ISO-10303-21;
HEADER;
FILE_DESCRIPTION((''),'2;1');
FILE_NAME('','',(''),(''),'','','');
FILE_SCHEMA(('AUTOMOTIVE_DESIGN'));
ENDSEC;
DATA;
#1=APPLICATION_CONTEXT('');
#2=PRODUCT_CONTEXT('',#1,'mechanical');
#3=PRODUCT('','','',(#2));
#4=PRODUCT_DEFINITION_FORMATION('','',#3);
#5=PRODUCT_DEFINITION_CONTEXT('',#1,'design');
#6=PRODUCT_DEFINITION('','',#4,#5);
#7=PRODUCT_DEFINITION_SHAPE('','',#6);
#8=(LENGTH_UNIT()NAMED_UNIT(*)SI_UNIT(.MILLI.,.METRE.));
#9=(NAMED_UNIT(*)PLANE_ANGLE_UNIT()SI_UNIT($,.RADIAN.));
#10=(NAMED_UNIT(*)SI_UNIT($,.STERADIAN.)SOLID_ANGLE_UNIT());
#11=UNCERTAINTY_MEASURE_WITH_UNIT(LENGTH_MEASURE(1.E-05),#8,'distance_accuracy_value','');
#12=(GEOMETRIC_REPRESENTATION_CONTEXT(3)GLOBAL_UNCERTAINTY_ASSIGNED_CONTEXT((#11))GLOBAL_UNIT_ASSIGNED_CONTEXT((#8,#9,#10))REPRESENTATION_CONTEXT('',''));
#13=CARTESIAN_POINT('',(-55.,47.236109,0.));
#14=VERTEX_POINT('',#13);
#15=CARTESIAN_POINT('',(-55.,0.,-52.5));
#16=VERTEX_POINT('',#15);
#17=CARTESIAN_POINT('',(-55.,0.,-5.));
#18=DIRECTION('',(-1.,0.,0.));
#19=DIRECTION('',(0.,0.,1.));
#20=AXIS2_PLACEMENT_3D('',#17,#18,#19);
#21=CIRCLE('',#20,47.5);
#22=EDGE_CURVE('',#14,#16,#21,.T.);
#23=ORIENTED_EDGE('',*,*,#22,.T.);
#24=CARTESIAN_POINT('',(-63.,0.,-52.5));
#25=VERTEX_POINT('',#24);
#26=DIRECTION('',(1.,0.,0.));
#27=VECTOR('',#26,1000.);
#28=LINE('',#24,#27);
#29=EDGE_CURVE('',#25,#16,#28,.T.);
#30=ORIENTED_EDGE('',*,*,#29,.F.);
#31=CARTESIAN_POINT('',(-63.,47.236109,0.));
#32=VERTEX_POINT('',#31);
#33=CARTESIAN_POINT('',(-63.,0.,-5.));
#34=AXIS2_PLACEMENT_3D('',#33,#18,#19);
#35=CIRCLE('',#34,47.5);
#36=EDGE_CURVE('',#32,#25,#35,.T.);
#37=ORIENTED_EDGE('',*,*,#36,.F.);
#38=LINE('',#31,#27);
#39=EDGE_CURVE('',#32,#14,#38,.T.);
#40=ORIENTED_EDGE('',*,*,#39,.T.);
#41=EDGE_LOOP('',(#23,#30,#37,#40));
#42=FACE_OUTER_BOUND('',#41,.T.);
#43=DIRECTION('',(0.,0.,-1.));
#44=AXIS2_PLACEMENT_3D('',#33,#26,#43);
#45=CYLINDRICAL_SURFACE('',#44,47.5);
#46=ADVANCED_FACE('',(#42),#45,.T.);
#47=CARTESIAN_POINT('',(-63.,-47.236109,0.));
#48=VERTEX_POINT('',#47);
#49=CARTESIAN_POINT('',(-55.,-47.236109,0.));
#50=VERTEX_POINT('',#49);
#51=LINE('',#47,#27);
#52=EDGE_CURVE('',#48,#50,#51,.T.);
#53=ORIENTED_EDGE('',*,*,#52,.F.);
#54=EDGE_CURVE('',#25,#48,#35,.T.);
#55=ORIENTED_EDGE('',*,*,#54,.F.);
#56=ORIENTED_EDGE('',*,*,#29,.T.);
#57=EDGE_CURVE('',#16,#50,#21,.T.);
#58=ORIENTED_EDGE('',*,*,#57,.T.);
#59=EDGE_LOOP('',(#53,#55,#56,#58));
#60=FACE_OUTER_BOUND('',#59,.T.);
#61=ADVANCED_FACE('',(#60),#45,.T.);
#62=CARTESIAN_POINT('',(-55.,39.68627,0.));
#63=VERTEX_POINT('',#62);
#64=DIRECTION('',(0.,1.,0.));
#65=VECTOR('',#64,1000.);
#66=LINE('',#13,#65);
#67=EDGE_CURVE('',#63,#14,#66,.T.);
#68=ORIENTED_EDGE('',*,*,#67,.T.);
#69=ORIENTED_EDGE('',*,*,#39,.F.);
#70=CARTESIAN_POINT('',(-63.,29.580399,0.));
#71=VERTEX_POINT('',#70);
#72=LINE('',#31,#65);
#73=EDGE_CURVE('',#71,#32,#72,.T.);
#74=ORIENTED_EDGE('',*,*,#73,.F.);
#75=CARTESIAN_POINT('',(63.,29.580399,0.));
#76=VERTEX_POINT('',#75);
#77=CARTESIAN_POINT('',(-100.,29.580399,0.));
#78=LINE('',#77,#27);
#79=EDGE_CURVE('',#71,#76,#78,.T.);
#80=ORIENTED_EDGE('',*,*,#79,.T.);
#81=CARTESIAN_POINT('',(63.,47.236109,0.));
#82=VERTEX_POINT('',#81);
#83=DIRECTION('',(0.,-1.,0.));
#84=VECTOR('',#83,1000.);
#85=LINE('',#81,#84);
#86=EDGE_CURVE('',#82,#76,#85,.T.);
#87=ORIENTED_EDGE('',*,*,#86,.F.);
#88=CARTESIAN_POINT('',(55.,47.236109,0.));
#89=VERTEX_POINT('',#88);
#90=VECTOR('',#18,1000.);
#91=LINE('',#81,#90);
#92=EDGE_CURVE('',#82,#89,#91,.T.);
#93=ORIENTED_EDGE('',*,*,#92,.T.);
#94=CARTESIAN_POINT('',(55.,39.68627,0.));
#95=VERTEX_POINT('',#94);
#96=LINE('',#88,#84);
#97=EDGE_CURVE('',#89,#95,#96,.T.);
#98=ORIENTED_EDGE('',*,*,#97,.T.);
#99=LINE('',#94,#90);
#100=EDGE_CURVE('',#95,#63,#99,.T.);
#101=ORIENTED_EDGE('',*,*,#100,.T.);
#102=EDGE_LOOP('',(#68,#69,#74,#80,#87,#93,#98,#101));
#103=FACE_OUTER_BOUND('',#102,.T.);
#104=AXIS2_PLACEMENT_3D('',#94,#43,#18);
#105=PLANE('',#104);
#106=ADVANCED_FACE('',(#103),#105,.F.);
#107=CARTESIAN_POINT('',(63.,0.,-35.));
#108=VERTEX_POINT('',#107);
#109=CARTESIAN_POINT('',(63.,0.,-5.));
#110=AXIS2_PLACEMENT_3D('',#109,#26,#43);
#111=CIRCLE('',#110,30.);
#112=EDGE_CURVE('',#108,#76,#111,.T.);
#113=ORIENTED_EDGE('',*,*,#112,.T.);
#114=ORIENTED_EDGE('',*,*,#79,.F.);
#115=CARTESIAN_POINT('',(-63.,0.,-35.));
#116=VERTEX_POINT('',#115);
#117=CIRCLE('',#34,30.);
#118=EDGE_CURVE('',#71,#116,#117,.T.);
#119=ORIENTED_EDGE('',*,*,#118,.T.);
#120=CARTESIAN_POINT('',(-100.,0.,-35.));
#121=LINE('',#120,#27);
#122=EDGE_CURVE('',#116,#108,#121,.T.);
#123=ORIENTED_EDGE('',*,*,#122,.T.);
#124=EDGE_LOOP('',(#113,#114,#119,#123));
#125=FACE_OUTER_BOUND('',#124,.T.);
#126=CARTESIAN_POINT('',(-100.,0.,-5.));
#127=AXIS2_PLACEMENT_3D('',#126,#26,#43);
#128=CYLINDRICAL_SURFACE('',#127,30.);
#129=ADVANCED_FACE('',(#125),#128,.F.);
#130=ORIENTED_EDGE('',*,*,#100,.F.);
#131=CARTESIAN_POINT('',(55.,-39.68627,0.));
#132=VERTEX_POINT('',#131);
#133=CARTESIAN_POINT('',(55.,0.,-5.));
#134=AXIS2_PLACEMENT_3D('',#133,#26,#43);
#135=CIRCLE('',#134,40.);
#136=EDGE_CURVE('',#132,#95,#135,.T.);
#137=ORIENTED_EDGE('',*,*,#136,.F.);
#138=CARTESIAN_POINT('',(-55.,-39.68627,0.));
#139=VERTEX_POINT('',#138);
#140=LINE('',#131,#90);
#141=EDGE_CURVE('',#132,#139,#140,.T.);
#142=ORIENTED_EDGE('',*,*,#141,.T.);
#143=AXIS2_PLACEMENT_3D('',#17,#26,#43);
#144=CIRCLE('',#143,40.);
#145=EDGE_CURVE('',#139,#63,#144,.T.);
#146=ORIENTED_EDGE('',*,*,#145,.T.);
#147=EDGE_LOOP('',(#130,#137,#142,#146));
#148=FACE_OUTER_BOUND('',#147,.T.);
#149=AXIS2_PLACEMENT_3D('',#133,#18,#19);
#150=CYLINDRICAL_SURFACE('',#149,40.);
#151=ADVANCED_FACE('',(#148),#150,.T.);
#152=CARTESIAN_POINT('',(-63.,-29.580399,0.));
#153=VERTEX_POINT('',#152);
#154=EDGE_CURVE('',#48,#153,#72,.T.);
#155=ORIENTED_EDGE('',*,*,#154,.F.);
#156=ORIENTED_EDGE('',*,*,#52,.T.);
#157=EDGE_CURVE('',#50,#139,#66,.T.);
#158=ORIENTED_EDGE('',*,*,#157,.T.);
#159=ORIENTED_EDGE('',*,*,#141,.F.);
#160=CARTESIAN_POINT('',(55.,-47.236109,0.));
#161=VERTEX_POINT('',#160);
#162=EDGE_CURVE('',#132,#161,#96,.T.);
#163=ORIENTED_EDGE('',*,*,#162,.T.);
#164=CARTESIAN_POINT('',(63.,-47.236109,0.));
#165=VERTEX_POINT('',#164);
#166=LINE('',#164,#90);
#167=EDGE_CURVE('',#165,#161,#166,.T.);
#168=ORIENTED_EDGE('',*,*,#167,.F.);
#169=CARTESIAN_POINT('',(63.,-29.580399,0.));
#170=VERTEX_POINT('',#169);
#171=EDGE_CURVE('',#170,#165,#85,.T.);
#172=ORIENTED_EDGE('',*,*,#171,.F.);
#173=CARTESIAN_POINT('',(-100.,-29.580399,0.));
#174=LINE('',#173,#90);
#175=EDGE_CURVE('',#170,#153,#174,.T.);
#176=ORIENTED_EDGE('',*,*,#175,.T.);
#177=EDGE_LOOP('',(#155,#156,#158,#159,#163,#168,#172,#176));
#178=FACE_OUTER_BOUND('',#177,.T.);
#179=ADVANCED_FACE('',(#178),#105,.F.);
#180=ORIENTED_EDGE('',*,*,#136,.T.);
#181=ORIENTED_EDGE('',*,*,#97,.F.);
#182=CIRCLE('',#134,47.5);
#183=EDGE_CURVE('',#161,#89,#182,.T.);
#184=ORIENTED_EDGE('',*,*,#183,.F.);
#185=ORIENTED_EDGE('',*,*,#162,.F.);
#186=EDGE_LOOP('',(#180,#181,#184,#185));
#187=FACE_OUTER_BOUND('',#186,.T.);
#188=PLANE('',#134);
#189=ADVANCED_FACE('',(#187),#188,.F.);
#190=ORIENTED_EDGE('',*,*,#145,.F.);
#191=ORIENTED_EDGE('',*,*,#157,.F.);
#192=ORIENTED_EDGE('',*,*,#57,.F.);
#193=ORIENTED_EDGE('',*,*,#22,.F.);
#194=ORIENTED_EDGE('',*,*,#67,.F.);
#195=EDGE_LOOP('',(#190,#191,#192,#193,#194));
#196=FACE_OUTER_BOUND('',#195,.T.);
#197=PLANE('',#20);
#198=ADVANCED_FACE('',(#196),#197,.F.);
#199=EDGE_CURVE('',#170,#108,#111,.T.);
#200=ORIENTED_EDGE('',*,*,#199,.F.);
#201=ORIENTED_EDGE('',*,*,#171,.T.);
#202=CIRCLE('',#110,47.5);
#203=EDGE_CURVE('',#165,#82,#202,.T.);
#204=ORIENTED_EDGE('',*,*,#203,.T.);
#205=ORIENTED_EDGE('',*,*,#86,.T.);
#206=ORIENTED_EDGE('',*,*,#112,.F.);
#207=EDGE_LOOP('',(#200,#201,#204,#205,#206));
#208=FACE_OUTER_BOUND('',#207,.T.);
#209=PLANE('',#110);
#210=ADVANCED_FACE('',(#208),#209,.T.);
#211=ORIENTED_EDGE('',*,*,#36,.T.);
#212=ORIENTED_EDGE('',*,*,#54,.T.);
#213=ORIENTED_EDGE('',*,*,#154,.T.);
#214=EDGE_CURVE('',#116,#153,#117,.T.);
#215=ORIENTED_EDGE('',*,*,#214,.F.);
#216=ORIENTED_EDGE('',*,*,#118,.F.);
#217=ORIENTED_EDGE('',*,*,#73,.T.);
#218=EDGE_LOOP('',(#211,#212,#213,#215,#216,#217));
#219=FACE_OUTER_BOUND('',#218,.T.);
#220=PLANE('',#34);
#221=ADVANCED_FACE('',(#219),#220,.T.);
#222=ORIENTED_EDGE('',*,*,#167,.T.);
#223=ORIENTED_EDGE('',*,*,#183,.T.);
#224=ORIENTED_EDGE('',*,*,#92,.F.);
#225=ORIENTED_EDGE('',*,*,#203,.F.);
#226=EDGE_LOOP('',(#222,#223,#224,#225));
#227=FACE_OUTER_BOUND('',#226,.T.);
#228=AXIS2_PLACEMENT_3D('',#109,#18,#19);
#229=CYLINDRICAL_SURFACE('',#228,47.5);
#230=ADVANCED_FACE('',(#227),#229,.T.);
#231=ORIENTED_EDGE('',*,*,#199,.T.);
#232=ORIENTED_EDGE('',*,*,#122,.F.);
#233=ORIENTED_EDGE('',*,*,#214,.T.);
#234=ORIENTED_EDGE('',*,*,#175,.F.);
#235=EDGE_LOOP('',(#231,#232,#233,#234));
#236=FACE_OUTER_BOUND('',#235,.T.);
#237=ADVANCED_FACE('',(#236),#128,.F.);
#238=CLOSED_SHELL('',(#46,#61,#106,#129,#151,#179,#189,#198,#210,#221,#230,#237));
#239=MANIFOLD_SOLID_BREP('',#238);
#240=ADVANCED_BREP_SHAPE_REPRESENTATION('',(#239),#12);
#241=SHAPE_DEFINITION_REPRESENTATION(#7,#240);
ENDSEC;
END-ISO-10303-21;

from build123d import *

# Parameters (mm, degrees)
HALF_SHELL_BODY_DEPTH   = 55
END_FLANGE_B_95X8_DEPTH = 8
END_START               = 8
END_FLANGE_A_95X8_DEPTH = 8
BORE_SKETCH_60_R        = 30
BORE_CUT_60_DEPTH       = 100


with BuildPart() as part:
    # Half Shell Profile Sketch → Half Shell Body (new, symmetric)
    with BuildSketch(Plane(origin=(0, 0, 0), x_dir=(0, 0, -1), z_dir=(1, 0, 0))):
        with BuildLine():
            Line((0, 39.686269666), (0, -39.686269666))
            ThreePointArc((0, -39.686269666), (45, 0), (0, 39.686269666))
        make_face()
    extrude(amount=HALF_SHELL_BODY_DEPTH, both=True)

    # End Flange B Sketch Ø95 → End Flange B Ø95x8 (add)
    with BuildSketch(Plane(origin=(55, 0, 0), x_dir=(0, 0, -1), z_dir=(1, 0, 0))):
        with BuildLine():
            Line((0, 47.236109069), (0, -47.236109069))
            ThreePointArc((0, -47.236109069), (52.5, 0), (0, 47.236109069))
        make_face()
    extrude(amount=END_FLANGE_B_95X8_DEPTH)

    # End Flange A Sketch Ø95 → End Flange A Ø95x8 (add)
    with BuildSketch(Plane.ZY.offset(55).offset(END_START)):
        with BuildLine():
            Line((0, 47.236109069), (0, -47.236109069))
            ThreePointArc((0, -47.236109069), (-52.5, 0), (0, 47.236109069))
        make_face()
    extrude(amount=-END_FLANGE_A_95X8_DEPTH)

    # Bore Sketch Ø60 → Bore Cut Ø60 (cut, symmetric)
    with BuildSketch(Plane(origin=(0, 0, 0), x_dir=(0, 0, -1), z_dir=(1, 0, 0))):
        with Locations((5, 0)):
            Circle(BORE_SKETCH_60_R)
    extrude(amount=BORE_CUT_60_DEPTH, both=True, mode=Mode.SUBTRACT)


solid = part.part
